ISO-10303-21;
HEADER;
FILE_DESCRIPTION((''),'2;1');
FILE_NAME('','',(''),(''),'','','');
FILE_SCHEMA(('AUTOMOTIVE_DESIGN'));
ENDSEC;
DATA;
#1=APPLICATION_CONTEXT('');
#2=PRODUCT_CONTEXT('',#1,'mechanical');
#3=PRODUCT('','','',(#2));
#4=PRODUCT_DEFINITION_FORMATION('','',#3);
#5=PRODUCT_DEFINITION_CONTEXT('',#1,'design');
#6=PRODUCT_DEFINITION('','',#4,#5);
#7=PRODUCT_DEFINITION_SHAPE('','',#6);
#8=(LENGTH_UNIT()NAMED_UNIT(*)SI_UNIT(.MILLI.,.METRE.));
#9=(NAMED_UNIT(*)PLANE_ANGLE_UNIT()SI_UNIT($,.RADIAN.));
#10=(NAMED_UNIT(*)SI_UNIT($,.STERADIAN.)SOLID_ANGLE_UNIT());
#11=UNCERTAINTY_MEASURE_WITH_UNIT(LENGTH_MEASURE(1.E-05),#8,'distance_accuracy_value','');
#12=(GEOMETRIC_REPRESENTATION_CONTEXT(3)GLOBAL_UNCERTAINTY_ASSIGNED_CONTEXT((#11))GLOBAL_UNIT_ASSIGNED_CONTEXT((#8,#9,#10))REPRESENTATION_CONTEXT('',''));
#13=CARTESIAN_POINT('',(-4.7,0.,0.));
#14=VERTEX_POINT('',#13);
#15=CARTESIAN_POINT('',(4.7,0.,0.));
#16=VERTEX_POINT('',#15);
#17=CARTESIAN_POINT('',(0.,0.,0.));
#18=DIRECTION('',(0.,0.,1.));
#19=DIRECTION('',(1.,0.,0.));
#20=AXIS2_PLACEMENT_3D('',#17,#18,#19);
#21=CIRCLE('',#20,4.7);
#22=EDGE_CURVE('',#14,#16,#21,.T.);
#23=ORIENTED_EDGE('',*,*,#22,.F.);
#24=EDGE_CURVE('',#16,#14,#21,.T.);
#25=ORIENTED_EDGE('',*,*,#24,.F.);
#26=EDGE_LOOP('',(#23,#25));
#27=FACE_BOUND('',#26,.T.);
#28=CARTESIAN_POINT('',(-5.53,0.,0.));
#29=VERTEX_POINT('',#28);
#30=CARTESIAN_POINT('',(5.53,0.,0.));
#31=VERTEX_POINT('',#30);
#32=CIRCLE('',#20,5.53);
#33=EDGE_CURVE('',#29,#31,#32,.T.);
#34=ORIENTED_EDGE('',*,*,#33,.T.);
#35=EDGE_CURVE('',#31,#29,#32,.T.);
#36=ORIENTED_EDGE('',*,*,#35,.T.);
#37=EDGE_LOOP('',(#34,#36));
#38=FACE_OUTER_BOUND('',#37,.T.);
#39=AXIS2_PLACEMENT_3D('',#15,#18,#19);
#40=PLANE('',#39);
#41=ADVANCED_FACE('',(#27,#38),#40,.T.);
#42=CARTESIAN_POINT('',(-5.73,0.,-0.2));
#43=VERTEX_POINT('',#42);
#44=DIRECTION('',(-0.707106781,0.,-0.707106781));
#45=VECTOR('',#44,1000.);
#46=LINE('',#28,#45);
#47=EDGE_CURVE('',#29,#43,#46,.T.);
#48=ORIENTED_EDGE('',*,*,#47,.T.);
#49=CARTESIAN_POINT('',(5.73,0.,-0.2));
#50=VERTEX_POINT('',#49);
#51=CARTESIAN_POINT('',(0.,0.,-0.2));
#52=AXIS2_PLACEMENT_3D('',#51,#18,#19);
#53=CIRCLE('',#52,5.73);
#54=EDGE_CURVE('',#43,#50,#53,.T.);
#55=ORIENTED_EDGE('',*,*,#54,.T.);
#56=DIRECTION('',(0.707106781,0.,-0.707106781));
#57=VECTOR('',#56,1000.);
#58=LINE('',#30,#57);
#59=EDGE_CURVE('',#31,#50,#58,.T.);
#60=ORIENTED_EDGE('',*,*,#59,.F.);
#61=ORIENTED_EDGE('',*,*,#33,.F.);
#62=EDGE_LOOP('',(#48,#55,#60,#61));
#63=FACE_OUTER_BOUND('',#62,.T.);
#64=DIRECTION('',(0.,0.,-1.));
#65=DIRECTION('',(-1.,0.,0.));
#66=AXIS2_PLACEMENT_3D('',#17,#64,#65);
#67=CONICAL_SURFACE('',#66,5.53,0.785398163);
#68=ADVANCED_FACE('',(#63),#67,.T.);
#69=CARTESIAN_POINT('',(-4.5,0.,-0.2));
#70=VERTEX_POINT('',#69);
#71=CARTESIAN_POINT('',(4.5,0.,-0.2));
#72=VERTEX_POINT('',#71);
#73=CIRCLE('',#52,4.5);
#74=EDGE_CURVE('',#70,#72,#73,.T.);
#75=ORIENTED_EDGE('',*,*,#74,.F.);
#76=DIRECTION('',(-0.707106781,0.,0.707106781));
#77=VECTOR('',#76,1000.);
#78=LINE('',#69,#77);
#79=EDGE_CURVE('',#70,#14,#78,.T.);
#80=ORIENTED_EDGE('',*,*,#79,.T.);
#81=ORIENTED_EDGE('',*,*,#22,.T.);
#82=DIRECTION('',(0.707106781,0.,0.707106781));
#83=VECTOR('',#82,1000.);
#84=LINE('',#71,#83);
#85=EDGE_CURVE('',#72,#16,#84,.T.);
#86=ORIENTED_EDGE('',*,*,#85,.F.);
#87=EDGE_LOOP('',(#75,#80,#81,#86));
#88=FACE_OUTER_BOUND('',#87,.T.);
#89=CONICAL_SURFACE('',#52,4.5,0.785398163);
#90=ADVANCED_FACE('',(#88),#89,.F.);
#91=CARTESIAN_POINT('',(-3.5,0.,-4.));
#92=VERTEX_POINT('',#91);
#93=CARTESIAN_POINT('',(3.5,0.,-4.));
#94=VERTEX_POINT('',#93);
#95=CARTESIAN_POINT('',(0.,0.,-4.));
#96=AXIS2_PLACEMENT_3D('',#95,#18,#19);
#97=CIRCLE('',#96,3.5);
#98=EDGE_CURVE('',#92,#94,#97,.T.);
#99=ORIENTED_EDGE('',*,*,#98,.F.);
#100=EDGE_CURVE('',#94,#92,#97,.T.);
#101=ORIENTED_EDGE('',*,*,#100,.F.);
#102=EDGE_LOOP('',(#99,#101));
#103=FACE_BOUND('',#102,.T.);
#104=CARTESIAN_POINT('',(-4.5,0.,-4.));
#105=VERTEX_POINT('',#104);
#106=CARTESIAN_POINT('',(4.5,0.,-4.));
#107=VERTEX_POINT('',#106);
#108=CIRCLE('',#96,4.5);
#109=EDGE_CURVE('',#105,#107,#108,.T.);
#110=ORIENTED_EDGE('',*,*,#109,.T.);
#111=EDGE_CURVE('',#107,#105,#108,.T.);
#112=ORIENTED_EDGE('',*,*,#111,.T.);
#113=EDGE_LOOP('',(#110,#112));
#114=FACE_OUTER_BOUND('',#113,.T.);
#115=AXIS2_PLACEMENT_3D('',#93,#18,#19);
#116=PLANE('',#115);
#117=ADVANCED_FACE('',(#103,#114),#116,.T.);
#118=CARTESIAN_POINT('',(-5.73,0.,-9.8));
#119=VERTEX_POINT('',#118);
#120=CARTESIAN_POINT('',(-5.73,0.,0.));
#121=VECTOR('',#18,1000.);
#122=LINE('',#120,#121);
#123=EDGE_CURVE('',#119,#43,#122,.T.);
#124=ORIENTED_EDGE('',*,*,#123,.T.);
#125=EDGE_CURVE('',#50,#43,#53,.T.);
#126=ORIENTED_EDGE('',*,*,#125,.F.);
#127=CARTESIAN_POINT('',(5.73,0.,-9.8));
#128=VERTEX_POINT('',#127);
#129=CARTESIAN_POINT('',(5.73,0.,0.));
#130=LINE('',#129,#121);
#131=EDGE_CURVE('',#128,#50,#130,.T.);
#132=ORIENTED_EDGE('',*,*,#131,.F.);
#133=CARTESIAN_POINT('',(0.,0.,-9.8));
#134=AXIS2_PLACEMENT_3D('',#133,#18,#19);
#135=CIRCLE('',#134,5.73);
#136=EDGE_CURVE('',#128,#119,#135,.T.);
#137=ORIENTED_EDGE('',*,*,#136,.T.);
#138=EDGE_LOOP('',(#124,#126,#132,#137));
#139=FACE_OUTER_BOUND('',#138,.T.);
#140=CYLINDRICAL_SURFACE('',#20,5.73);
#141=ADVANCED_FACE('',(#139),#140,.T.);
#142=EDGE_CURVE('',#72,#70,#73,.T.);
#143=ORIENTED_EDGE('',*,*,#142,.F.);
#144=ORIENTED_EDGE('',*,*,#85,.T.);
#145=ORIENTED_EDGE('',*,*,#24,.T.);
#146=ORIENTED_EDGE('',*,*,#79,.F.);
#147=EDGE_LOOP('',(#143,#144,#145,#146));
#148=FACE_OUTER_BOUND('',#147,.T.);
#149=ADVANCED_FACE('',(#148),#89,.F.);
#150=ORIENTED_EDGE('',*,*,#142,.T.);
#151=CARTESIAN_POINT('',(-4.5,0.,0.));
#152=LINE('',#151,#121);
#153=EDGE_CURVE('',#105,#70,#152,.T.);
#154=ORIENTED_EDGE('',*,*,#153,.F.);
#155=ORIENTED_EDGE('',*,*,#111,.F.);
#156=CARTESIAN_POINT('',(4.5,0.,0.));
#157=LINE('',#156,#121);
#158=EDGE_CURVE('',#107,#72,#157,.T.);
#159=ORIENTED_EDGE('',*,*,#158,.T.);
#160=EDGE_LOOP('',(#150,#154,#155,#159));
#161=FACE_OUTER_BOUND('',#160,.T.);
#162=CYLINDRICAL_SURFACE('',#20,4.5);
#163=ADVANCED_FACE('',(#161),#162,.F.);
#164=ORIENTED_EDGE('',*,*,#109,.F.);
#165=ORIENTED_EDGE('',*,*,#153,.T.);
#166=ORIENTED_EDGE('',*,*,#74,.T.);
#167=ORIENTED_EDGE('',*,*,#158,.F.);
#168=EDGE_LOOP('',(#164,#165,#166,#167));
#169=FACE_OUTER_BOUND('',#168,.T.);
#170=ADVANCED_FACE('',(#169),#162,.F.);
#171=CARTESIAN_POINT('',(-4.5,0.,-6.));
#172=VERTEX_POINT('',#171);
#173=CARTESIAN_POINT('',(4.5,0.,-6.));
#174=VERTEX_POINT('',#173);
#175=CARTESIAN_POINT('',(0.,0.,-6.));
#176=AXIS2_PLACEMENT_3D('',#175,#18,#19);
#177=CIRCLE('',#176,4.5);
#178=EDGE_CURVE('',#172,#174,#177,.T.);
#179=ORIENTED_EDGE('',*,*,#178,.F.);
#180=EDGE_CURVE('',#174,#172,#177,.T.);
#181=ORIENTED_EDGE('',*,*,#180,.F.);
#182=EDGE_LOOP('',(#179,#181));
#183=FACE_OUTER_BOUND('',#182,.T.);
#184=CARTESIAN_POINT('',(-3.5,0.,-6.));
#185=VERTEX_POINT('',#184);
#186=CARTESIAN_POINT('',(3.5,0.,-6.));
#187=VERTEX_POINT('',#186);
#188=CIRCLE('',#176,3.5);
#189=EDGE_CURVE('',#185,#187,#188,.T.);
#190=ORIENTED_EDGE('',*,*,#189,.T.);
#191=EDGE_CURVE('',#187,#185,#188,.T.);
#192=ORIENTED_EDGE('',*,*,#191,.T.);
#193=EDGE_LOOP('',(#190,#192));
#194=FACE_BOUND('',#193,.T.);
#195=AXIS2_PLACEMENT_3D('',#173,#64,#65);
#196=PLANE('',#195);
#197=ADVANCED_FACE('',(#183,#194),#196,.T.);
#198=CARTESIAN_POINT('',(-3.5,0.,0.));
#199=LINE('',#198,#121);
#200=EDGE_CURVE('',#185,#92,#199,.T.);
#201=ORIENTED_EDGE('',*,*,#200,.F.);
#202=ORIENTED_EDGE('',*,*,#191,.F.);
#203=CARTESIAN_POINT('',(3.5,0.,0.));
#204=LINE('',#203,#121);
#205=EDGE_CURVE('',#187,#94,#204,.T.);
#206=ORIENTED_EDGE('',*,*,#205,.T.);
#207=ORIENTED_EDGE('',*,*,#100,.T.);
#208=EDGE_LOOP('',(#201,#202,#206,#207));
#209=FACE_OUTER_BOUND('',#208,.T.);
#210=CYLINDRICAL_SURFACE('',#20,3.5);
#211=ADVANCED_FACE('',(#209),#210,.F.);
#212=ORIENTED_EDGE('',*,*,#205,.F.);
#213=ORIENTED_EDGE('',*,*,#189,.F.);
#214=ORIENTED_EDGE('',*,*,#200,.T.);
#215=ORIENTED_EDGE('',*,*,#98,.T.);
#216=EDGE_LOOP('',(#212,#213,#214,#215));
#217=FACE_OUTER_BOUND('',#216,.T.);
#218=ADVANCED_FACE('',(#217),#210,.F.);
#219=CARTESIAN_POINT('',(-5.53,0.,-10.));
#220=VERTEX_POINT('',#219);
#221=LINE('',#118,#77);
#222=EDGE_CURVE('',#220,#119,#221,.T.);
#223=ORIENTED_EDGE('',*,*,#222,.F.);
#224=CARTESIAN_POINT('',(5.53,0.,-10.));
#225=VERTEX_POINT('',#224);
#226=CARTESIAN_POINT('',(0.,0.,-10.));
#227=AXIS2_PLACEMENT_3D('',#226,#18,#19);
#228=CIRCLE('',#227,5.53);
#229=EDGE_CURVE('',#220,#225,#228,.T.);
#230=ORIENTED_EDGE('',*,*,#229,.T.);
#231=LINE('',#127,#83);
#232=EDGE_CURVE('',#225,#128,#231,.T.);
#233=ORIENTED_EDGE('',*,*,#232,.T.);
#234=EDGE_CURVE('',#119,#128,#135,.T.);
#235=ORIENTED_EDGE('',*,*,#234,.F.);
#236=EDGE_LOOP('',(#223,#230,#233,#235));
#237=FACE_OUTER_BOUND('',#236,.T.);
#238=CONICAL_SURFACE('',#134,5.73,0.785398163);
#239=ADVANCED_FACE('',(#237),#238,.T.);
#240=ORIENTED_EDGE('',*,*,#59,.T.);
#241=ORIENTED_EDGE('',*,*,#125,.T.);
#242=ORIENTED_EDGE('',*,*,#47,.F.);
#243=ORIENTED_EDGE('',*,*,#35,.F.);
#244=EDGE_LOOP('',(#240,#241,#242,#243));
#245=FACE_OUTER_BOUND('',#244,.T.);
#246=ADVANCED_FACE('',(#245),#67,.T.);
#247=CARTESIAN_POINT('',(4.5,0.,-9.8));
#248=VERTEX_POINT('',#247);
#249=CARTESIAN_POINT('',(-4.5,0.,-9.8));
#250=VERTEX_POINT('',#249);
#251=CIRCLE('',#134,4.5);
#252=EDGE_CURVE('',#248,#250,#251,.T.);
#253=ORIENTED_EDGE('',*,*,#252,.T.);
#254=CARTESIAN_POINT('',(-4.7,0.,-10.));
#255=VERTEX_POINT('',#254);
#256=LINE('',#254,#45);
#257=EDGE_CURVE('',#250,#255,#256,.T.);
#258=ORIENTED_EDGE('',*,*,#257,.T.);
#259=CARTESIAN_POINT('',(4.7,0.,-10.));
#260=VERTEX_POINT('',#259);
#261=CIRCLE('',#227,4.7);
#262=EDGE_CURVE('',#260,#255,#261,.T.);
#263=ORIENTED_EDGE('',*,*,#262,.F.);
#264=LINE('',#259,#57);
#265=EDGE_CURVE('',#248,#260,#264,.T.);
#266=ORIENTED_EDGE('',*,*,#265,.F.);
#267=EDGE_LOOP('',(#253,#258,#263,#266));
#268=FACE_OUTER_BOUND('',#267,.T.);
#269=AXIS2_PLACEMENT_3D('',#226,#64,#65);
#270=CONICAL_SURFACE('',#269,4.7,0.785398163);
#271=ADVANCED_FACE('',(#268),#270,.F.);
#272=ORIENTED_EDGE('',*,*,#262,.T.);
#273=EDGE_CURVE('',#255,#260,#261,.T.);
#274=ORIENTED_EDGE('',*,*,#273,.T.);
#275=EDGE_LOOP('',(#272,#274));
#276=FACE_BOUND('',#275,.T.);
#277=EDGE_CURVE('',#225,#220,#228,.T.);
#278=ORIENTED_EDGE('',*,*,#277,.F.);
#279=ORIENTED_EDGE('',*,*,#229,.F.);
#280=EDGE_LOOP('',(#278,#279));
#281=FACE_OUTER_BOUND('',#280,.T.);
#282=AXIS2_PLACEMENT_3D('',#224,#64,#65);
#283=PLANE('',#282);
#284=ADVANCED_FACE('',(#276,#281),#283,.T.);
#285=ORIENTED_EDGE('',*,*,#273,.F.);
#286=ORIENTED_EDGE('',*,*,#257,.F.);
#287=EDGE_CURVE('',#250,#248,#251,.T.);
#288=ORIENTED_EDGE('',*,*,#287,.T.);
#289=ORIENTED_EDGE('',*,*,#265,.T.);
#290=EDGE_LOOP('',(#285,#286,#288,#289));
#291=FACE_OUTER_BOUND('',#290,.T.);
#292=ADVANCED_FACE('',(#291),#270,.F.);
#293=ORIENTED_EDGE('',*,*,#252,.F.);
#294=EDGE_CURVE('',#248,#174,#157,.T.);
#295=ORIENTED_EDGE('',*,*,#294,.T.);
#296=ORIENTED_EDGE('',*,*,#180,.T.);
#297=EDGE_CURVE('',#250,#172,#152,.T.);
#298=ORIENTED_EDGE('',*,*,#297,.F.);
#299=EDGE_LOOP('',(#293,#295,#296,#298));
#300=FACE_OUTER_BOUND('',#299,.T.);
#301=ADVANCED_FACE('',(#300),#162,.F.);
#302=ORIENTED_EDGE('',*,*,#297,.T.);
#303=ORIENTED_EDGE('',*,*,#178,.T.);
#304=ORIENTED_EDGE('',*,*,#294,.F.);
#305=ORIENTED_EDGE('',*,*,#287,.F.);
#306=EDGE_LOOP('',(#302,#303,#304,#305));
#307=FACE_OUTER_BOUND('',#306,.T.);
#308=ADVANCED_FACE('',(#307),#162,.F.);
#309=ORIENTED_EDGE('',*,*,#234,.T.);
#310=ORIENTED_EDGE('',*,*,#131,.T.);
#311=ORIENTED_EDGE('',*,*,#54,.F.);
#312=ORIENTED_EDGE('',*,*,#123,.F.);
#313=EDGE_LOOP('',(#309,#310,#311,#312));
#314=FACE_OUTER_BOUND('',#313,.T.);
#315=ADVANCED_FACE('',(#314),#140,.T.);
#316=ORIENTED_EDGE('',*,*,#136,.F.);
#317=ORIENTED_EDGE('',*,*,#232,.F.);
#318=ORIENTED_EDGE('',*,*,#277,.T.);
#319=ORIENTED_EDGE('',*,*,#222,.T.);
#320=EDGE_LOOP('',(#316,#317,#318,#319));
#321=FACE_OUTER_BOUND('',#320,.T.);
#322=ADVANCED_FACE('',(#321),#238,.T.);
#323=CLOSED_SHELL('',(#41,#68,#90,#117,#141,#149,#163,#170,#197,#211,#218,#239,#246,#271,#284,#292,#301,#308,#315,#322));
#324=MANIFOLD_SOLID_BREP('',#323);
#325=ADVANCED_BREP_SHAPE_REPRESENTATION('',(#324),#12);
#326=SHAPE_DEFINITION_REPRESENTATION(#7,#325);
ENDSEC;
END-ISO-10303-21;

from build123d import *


with BuildPart() as part:
    # Sketch1 → Revolve1 (revolve)
    with BuildSketch(Plane(origin=(0, 0, 0), x_dir=(1, 0, 0), z_dir=(0, 1, 0))):
        Polygon((4.7, 0), (5.53, 0), (5.73, 0.2), (5.73, 9.8), (5.53, 10), (4.7, 10), (4.5, 9.8), (4.5, 6), (3.5, 6), (3.5, 4), (4.5, 4), (4.5, 0.2), align=None)
    revolve(axis=Axis((0, 0, 0), (0, 0, -1)))


solid = part.part
